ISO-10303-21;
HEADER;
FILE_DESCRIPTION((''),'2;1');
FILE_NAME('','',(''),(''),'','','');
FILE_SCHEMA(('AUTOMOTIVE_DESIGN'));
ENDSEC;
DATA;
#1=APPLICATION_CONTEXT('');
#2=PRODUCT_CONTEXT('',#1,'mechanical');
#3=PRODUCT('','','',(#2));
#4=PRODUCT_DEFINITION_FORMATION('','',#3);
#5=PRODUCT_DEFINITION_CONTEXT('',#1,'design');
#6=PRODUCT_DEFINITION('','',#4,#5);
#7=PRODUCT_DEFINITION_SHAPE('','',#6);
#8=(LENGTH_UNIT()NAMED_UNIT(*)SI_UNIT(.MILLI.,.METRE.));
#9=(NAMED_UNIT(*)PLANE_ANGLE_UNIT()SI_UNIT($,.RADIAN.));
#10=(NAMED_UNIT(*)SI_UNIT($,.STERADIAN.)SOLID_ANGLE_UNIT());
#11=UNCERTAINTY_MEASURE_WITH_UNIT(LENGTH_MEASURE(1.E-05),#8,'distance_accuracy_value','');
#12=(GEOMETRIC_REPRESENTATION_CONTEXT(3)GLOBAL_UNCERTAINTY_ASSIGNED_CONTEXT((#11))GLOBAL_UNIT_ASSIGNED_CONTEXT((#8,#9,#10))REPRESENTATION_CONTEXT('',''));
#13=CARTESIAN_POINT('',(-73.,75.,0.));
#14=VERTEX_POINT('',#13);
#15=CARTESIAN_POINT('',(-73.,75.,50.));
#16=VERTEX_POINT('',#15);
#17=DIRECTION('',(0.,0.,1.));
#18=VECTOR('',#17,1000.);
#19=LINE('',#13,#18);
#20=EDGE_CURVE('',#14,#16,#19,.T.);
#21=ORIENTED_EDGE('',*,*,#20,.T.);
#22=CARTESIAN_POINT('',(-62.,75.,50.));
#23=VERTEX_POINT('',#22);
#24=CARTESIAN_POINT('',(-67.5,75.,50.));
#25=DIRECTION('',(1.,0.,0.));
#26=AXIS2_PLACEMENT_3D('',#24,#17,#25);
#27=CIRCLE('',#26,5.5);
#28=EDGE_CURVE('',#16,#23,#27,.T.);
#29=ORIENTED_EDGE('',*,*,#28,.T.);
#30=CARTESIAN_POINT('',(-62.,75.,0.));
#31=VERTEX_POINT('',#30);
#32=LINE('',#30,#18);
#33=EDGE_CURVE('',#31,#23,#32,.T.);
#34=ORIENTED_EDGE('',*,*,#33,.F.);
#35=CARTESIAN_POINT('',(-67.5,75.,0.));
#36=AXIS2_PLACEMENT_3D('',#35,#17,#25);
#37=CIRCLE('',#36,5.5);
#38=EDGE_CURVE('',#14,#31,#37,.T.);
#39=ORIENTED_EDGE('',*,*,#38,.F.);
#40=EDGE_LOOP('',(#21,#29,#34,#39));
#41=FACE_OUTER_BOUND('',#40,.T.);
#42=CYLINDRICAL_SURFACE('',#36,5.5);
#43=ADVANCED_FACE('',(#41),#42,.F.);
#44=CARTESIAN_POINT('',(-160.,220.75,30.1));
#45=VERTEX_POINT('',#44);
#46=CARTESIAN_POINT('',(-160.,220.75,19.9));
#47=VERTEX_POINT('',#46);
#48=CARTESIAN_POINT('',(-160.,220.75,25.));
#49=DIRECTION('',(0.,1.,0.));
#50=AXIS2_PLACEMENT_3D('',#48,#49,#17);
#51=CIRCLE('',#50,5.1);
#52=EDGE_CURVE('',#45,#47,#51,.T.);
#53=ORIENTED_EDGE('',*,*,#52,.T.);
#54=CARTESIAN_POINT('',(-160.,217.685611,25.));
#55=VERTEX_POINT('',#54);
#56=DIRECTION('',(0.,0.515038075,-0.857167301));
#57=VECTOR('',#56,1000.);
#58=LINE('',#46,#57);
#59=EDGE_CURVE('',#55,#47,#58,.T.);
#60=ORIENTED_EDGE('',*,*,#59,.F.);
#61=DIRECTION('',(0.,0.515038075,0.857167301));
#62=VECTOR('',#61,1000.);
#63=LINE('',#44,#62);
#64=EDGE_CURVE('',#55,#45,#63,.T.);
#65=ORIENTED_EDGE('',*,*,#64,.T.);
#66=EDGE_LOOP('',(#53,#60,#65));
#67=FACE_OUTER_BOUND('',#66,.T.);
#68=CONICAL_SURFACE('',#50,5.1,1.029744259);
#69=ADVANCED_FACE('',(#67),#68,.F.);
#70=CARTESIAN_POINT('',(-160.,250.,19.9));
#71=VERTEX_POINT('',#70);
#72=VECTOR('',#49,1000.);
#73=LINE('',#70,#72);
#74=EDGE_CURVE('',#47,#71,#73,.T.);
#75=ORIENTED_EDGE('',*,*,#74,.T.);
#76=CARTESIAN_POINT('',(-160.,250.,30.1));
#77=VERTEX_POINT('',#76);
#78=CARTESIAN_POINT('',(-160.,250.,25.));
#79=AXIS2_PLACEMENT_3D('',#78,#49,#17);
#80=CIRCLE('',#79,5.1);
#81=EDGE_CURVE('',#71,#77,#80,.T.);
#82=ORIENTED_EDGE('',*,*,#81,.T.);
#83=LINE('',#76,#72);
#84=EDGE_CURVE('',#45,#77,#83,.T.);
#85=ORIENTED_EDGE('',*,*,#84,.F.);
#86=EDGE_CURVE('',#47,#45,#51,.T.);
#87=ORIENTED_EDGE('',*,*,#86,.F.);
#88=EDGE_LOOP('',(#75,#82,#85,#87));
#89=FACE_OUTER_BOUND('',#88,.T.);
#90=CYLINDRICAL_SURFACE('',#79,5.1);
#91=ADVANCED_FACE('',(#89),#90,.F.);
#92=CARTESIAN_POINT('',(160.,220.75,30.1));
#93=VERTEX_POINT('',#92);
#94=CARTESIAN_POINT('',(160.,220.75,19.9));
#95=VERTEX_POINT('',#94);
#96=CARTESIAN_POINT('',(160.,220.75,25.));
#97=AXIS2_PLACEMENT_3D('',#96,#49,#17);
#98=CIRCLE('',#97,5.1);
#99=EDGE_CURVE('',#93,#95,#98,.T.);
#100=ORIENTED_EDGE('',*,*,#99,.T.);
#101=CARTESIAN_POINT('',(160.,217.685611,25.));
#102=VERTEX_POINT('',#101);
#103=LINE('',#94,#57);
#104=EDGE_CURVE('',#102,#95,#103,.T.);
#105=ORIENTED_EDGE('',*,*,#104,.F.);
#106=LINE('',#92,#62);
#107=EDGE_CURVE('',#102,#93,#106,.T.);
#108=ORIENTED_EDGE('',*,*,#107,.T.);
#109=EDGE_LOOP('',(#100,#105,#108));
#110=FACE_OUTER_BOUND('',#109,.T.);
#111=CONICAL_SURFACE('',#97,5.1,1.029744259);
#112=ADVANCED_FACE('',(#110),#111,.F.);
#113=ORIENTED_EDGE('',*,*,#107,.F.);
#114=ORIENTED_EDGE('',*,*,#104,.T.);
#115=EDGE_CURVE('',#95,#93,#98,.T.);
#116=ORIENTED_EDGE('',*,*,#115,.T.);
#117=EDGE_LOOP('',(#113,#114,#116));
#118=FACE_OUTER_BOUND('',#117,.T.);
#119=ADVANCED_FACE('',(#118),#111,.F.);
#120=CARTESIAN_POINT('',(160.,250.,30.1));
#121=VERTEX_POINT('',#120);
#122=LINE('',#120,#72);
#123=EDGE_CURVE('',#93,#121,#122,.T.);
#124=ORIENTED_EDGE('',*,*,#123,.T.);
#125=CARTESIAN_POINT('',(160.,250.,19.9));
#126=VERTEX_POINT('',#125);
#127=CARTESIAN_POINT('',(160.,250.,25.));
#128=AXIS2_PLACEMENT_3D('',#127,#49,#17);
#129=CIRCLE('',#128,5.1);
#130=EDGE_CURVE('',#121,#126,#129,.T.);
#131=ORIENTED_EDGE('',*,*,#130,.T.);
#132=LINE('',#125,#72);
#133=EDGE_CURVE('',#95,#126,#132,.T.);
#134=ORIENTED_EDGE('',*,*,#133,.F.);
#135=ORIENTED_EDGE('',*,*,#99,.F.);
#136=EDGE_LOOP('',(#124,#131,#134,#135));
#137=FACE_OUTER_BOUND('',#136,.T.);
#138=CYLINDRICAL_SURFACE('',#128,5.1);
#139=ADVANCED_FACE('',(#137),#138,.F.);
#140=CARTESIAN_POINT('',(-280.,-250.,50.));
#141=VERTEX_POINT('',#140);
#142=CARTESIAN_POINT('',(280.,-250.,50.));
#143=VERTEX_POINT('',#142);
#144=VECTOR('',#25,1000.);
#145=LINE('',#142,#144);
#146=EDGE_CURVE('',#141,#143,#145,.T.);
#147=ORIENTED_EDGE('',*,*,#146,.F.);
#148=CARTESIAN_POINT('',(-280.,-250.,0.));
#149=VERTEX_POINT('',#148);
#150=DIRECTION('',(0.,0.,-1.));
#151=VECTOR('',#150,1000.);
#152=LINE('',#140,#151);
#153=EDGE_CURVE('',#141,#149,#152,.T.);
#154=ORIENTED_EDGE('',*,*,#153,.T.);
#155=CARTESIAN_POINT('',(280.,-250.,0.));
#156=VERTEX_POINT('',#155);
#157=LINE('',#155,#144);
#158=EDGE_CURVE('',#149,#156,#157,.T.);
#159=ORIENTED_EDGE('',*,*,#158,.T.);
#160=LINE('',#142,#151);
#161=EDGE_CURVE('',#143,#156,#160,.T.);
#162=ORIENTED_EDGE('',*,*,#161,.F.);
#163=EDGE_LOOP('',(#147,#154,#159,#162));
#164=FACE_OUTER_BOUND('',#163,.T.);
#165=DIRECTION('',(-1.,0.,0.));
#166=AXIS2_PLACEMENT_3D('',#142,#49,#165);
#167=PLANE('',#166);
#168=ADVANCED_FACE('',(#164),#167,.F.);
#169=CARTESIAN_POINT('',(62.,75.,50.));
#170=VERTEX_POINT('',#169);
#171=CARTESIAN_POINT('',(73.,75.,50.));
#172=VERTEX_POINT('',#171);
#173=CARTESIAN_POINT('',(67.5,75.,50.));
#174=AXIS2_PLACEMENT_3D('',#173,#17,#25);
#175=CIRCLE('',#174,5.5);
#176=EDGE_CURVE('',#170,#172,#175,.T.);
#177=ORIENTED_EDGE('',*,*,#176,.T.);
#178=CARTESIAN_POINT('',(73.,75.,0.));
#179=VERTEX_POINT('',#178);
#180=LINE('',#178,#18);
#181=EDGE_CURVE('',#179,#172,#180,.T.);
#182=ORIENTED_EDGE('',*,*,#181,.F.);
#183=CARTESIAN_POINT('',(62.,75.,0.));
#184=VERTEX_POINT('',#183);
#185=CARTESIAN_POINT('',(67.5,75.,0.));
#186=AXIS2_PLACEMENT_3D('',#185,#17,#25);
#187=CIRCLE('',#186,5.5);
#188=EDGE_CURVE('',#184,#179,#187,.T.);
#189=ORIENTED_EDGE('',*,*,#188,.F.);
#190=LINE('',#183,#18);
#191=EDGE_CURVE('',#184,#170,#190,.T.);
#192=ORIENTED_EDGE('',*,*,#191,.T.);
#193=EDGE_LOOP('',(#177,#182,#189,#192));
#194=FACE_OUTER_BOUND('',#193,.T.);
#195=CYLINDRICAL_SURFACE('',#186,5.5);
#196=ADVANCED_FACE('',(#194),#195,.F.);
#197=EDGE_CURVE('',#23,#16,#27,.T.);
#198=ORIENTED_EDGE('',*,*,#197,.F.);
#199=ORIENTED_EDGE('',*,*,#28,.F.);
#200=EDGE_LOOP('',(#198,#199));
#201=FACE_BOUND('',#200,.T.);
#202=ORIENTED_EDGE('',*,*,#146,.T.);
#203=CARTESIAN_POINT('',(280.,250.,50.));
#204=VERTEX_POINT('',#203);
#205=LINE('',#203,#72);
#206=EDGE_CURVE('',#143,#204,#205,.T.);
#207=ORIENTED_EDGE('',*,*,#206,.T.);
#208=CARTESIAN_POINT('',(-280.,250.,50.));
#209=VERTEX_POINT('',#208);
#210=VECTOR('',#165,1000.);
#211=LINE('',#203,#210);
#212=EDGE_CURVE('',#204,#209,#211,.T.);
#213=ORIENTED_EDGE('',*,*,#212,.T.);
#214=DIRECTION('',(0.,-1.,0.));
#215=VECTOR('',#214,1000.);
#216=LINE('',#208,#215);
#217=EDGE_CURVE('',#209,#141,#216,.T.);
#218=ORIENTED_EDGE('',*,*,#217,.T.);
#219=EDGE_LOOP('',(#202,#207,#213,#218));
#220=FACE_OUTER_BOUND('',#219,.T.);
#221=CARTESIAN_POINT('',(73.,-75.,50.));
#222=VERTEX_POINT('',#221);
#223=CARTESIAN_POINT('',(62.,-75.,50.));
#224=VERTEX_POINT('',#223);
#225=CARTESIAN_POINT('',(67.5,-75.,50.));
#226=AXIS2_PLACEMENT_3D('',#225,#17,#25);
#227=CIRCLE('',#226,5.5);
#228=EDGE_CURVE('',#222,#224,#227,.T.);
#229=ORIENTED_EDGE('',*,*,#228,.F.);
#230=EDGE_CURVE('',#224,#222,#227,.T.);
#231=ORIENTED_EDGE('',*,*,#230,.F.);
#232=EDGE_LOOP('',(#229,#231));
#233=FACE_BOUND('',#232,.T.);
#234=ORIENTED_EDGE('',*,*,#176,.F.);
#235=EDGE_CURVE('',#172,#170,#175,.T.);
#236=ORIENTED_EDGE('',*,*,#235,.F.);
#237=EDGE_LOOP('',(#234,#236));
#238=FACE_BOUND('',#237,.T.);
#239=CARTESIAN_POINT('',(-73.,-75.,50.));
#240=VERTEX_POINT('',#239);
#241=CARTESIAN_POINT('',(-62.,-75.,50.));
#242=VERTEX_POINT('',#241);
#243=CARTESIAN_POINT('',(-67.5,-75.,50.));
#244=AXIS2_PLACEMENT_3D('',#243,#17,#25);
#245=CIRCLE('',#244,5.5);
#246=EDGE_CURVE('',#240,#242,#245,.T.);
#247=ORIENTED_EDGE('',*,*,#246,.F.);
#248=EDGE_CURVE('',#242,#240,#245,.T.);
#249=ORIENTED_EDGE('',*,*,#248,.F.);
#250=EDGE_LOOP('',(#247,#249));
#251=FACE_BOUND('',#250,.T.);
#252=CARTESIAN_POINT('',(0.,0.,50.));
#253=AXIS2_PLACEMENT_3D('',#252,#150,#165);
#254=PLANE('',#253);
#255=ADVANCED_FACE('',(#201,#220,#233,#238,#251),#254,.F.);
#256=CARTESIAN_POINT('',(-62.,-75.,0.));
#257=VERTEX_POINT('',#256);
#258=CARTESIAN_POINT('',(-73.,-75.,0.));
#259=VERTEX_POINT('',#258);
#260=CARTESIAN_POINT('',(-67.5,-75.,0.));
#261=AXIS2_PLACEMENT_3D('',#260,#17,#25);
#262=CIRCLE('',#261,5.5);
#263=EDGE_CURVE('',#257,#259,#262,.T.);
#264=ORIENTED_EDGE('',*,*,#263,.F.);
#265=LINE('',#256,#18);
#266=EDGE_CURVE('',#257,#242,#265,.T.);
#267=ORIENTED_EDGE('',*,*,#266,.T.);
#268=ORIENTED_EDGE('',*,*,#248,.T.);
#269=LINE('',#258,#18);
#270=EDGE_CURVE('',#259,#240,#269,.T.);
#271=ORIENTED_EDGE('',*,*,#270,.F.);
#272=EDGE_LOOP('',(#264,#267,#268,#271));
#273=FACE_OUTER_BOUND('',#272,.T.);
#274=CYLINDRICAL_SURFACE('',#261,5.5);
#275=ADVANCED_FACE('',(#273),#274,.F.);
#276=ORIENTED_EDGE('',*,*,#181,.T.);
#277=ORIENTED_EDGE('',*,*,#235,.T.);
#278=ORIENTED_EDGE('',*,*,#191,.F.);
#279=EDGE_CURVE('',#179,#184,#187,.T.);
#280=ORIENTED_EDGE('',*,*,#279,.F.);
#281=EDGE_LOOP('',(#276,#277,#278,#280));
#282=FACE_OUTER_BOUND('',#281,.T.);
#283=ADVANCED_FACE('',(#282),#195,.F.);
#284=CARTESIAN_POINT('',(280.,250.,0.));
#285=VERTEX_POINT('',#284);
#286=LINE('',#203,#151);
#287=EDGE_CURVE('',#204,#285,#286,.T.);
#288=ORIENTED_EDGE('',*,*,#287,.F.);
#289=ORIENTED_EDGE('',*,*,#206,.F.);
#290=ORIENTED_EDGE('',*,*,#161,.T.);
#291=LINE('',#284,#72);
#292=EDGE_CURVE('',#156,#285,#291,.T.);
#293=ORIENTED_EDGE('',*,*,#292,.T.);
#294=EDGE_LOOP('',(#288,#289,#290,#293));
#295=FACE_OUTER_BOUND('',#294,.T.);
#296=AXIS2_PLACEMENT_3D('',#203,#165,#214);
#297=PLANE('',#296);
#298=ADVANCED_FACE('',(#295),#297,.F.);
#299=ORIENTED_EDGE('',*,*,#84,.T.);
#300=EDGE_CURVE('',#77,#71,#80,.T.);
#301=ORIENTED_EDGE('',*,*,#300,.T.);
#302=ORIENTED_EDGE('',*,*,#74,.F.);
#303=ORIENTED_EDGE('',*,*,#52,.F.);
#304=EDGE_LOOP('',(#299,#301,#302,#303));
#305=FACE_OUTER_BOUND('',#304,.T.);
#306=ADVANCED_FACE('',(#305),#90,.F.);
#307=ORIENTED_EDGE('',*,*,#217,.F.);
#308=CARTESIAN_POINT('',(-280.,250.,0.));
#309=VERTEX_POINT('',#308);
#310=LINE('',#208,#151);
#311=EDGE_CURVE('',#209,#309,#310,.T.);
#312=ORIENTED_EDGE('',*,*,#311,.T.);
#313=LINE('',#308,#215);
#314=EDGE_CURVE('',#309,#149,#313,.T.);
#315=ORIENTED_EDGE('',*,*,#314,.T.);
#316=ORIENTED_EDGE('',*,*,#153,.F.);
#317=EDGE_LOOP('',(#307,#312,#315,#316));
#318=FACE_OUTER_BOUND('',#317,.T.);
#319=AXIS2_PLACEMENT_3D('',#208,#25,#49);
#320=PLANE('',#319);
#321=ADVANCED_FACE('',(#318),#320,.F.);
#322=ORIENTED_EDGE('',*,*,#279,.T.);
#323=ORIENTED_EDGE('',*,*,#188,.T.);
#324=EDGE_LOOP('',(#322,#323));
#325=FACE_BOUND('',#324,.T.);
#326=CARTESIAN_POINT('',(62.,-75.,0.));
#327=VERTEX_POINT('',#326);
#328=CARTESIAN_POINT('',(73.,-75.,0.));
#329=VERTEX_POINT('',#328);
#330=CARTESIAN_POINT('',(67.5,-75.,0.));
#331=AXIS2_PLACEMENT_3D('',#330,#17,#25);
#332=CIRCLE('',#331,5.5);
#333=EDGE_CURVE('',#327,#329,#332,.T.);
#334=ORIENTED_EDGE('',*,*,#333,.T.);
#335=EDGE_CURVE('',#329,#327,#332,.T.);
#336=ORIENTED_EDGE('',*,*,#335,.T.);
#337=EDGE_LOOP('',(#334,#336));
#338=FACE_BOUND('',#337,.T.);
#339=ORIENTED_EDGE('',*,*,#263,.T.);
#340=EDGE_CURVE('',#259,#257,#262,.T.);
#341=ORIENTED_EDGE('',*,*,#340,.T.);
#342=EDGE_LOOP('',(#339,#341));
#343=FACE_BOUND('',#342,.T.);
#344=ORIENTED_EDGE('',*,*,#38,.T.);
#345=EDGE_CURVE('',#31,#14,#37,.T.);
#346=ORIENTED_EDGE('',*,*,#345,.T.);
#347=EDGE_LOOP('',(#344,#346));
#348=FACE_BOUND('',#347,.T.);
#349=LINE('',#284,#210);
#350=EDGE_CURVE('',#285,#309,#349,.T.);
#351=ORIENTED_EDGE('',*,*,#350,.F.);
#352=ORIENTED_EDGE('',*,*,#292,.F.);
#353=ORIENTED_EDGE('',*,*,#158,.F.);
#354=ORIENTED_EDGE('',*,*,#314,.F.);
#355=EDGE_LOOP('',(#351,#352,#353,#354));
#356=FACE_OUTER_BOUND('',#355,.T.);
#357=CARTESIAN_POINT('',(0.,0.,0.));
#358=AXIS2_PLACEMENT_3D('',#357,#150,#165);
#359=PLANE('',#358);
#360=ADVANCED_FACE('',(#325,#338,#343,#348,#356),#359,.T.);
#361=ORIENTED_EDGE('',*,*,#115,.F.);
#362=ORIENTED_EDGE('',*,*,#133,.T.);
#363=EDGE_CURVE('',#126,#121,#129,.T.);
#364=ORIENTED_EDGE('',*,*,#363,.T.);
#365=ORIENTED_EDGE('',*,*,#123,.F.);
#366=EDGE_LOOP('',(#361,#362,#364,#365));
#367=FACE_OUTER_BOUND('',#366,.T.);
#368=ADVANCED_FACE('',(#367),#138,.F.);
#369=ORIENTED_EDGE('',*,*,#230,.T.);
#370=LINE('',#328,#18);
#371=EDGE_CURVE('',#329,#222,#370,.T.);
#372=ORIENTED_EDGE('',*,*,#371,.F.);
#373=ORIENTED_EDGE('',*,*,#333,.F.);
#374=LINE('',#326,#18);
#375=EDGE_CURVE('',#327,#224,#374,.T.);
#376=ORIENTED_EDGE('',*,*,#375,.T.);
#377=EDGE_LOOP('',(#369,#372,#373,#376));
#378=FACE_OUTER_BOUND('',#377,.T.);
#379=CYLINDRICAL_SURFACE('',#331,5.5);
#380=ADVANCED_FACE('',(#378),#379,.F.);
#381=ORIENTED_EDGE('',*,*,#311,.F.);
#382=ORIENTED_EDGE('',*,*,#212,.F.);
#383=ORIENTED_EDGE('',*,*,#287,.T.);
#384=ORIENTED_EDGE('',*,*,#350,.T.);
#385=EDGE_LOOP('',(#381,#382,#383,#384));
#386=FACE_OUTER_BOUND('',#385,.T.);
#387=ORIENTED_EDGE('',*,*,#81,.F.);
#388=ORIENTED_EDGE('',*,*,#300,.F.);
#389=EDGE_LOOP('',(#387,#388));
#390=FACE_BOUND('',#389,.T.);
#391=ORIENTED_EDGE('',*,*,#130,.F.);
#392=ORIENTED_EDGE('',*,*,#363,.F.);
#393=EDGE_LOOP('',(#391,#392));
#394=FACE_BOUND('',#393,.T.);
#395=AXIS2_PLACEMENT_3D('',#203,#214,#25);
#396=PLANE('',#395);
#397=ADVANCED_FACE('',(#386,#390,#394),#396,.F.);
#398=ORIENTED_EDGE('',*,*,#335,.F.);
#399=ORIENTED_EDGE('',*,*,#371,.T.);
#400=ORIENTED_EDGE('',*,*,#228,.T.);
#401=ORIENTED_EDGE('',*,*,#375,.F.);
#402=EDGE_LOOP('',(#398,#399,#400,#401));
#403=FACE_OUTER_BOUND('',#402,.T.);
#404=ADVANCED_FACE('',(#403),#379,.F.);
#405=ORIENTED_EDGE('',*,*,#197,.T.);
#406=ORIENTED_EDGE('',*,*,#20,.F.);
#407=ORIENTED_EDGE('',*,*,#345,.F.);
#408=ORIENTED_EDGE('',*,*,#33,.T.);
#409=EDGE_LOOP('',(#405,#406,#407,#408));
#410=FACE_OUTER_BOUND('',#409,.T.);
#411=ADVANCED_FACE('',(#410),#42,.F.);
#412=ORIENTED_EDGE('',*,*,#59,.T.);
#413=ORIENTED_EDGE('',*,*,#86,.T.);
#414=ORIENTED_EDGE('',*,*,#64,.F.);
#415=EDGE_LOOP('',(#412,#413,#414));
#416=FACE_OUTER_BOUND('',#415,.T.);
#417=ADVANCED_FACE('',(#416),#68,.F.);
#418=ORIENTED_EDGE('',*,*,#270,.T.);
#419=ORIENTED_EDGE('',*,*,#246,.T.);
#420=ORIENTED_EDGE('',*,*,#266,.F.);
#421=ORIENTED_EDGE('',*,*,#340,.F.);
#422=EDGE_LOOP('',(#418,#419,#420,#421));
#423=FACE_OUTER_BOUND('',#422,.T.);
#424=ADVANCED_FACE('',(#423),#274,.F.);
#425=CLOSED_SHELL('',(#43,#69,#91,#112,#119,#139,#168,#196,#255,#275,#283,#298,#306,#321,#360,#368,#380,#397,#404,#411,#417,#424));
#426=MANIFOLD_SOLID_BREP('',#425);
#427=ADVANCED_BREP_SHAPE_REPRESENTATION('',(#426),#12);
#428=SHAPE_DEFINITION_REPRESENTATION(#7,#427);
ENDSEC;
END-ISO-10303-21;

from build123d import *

# Parameters (mm, degrees)
SKETCH_1_W              = 560
SKETCH_1_H              = 500
EXTRUDE_1_DEPTH         = 50
HOLE_WIZARD_M12_1_D     = 10.2
HOLE_WIZARD_M12_1_DEPTH = 29.25
HOLE_WIZARD_M12_1_TIP   = 3.064389157
SKETCH_5_R              = 5.5
CUT_EXTRUDE_1_DEPTH     = 50


with BuildPart() as part:
    # 草图1 → 凸台-拉伸1 (new body)
    with BuildSketch(Plane.XY):
        Rectangle(SKETCH_1_W, SKETCH_1_H)
    extrude(amount=EXTRUDE_1_DEPTH)

    # M12 螺纹孔1
    with Locations(Plane(origin=(0, 250, 0), x_dir=(1, 0, 0), z_dir=(0, 1, 0))):
        with Locations((-160, -25), (160, -25)):
            Hole(HOLE_WIZARD_M12_1_D / 2, depth=HOLE_WIZARD_M12_1_DEPTH)
            with Locations((0, 0, -(HOLE_WIZARD_M12_1_DEPTH + HOLE_WIZARD_M12_1_TIP / 2))):  # 118° drill point
                Cone(0, HOLE_WIZARD_M12_1_D / 2, HOLE_WIZARD_M12_1_TIP, mode=Mode.SUBTRACT)

    # 草图5 → 切除-拉伸1 (cut)
    with BuildSketch(Plane.XY.offset(50)):
        with Locations((-67.5, 75)):
            Circle(SKETCH_5_R)
        with Locations((67.5, 75)):
            Circle(SKETCH_5_R)
        with Locations((67.5, -75)):
            Circle(SKETCH_5_R)
        with Locations((-67.5, -75)):
            Circle(SKETCH_5_R)
    extrude(amount=-CUT_EXTRUDE_1_DEPTH, mode=Mode.SUBTRACT)


solid = part.part
